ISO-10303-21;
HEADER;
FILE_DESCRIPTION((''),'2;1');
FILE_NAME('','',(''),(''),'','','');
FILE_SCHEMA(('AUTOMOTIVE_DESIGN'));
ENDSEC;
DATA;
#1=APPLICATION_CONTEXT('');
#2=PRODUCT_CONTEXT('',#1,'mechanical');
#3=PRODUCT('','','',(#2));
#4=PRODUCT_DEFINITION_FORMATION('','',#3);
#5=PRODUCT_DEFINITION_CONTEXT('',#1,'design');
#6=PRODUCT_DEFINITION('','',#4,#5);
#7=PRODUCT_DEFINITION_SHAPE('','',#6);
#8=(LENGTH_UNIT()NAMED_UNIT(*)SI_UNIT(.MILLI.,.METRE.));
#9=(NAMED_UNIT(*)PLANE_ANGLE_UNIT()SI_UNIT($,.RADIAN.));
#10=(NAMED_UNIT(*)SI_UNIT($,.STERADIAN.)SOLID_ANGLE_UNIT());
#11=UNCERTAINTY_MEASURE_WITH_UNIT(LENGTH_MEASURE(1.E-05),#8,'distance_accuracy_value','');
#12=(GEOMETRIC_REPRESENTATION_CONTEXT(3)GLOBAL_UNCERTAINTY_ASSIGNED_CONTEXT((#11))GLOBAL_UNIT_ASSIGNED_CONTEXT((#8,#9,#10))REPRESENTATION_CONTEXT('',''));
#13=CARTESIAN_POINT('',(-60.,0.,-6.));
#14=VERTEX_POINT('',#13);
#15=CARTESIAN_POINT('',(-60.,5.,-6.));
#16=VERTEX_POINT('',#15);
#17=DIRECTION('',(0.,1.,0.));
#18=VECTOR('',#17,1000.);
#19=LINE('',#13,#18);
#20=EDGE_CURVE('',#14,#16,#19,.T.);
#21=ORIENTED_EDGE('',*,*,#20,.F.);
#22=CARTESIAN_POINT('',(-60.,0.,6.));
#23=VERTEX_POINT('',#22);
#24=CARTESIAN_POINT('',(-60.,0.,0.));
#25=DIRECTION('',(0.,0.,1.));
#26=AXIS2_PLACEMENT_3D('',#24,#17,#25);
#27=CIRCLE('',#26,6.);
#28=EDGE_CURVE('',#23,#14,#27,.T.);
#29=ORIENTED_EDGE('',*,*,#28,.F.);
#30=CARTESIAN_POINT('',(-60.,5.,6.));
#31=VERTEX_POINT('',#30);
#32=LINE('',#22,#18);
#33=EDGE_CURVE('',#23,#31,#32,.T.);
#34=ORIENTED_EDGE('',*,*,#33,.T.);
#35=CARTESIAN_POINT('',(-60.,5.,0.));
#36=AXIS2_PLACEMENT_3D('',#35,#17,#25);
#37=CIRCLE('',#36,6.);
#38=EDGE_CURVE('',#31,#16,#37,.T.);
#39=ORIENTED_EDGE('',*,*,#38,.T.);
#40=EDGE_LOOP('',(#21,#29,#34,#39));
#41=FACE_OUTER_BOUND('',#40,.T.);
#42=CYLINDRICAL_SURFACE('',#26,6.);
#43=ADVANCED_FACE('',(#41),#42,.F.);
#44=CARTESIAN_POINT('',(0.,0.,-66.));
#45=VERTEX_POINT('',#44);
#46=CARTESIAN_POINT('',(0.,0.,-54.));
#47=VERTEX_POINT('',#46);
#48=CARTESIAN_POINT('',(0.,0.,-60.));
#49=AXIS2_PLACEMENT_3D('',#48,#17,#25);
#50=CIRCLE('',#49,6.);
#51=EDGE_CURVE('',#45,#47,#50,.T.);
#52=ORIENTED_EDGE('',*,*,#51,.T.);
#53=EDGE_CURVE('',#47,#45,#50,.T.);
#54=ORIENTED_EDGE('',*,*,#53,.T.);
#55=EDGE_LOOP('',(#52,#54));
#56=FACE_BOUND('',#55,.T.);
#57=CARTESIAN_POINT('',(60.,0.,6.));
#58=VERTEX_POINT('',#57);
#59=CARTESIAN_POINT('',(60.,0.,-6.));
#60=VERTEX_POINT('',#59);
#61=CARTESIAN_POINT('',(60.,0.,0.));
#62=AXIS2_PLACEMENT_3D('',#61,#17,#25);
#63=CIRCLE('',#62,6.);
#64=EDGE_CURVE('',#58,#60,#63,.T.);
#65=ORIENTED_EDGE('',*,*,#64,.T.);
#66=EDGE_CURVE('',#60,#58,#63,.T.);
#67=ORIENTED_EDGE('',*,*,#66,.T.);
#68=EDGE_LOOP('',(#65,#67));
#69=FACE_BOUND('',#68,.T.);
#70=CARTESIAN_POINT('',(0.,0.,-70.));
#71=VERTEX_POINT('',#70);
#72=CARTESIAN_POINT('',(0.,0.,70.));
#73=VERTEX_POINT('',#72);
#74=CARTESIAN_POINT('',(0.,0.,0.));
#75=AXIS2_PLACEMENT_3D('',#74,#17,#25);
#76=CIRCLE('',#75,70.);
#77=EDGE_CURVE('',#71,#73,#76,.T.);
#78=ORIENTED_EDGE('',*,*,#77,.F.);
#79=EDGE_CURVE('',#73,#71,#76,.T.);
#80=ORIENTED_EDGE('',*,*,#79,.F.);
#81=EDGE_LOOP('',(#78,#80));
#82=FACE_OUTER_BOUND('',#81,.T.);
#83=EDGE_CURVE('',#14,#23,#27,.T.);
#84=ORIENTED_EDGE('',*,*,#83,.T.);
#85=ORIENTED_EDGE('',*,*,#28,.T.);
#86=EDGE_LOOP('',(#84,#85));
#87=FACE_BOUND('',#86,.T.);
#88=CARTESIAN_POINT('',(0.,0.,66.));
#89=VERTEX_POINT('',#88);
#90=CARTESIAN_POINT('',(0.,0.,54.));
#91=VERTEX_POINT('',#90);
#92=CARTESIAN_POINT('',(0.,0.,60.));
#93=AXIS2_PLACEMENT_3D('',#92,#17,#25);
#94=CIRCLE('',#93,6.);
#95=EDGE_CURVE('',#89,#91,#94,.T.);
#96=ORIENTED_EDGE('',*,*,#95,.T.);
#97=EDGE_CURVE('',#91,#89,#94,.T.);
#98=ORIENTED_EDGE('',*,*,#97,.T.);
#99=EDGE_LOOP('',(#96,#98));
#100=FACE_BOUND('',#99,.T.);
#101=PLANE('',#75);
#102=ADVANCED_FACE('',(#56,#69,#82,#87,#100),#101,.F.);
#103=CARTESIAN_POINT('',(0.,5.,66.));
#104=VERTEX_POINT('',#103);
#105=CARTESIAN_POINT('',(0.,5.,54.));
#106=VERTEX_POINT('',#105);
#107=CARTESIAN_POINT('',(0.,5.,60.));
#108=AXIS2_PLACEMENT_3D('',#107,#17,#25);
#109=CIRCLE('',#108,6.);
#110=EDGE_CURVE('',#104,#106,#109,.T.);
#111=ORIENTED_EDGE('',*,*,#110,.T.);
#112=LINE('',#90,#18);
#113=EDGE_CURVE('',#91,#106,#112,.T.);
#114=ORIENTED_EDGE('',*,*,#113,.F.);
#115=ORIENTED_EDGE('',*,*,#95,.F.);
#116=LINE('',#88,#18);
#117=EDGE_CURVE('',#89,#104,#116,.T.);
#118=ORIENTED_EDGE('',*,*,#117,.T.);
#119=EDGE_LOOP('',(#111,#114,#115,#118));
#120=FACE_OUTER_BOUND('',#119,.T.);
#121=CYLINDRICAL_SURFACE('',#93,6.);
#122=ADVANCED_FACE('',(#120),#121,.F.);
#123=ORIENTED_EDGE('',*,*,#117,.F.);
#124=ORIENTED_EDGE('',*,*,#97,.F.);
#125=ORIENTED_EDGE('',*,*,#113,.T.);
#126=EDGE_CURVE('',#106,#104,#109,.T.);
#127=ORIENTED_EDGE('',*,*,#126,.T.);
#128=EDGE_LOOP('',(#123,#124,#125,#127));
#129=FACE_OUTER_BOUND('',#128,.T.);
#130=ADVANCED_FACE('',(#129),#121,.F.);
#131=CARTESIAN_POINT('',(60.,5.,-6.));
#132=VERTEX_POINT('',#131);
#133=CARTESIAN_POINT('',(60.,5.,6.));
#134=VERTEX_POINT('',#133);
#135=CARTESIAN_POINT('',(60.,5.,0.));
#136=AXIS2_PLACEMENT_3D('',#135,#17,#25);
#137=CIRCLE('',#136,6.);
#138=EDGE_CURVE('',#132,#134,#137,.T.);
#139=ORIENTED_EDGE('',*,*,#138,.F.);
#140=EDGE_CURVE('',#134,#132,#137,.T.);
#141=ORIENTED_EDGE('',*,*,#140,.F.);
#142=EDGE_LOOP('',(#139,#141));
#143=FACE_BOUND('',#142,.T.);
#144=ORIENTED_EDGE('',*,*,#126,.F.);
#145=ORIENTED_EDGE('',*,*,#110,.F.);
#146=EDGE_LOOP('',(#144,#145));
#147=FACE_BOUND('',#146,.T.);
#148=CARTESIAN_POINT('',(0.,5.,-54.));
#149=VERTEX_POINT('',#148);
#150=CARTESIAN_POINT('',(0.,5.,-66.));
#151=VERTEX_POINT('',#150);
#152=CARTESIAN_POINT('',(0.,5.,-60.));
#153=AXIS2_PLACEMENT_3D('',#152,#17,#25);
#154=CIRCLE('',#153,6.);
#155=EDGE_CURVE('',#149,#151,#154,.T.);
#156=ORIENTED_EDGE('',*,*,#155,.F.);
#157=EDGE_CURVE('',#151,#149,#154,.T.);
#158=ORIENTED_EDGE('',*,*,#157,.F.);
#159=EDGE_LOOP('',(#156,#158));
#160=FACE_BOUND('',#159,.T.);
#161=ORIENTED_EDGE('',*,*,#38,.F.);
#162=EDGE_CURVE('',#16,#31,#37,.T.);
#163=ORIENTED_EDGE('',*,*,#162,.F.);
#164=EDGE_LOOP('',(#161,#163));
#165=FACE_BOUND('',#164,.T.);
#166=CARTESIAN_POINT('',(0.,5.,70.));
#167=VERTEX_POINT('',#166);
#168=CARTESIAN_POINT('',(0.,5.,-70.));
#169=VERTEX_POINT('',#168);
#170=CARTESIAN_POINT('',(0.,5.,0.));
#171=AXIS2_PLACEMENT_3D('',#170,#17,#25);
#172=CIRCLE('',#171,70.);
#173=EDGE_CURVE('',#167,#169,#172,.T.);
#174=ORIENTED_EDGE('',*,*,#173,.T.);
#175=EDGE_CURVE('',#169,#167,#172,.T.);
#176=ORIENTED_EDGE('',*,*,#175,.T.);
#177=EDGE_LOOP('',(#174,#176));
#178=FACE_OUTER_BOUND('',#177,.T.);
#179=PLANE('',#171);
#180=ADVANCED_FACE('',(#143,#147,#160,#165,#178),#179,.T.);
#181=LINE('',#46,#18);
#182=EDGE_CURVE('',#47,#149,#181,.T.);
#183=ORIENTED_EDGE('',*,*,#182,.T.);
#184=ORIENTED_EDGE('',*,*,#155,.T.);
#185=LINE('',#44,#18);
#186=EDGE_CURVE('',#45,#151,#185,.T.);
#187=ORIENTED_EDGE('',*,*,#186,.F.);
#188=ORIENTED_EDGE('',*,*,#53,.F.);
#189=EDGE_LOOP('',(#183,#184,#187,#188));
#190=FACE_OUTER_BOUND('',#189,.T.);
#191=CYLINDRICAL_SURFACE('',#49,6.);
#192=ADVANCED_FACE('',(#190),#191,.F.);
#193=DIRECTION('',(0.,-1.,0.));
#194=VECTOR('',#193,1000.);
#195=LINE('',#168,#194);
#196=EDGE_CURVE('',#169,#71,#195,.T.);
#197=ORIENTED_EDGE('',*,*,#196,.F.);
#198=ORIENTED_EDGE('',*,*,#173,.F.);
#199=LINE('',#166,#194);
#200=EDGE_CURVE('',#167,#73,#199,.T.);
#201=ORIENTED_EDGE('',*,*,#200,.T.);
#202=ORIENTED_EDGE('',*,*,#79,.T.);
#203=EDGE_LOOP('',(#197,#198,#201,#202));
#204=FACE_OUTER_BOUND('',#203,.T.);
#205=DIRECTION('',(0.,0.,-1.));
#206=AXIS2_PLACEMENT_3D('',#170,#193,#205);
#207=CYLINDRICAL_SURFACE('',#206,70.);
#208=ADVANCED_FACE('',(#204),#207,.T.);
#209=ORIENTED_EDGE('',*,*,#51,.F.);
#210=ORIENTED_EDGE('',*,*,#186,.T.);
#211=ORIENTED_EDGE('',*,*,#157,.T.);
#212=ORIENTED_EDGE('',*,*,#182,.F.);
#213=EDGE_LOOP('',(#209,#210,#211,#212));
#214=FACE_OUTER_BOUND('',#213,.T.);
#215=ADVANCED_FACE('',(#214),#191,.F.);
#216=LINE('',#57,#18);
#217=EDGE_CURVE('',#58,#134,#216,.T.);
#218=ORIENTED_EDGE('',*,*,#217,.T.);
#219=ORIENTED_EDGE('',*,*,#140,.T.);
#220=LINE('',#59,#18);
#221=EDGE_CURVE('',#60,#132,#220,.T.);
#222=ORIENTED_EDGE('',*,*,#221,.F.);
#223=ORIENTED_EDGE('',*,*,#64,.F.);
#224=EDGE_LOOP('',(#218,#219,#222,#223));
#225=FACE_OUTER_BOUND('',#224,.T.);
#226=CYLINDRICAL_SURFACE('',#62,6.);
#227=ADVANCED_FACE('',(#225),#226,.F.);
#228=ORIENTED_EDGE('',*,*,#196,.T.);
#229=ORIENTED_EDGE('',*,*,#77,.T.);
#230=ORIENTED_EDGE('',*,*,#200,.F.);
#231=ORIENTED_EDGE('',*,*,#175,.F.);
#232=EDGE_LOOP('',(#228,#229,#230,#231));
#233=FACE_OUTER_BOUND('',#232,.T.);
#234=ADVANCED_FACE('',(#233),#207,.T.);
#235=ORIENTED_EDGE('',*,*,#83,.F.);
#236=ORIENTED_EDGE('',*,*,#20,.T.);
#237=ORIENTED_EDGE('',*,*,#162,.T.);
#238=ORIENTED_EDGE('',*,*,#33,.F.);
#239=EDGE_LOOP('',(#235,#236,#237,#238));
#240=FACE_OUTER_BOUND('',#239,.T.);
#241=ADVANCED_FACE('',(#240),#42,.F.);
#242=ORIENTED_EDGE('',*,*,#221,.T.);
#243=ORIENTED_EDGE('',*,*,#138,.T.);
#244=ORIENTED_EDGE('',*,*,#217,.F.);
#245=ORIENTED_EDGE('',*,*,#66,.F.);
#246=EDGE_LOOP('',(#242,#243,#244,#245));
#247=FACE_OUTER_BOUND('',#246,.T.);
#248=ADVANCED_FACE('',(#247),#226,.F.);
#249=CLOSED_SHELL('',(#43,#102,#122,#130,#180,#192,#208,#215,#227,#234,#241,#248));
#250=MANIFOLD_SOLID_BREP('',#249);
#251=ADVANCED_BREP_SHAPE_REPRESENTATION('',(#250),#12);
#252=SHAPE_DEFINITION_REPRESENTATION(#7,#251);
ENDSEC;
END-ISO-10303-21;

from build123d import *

# Parameters (mm, degrees)
SKETCH_1_R          = 70
EXTRUDE_1_DEPTH     = 5
SKETCH_3_R          = 6
CUT_EXTRUDE_1_DEPTH = 100.121138008


with BuildPart() as part:
    # 草图1 → 凸台-拉伸1 (new body)
    with BuildSketch(Plane(origin=(0, 0, 0), x_dir=(1, 0, 0), z_dir=(0, 1, 0))):
        with Locations(Location((0, 0, 0), (0, 0, 270))):
            Circle(SKETCH_1_R)
    extrude(amount=EXTRUDE_1_DEPTH)

    # 草图3 → 切除-拉伸1 (cut, through all)
    with BuildSketch(Plane(origin=(0, 5, 0), x_dir=(1, 0, 0), z_dir=(0, 1, 0))):
        with Locations(Location((0, 60, 0), (0, 0, 270))):
            Circle(SKETCH_3_R)
        with Locations(Location((60, 0, 0), (0, 0, 270))):
            Circle(SKETCH_3_R)
        with Locations(Location((0, -60, 0), (0, 0, 270))):
            Circle(SKETCH_3_R)
        with Locations(Location((-60, 0, 0), (0, 0, 270))):
            Circle(SKETCH_3_R)
    extrude(amount=-CUT_EXTRUDE_1_DEPTH, mode=Mode.SUBTRACT)


solid = part.part
